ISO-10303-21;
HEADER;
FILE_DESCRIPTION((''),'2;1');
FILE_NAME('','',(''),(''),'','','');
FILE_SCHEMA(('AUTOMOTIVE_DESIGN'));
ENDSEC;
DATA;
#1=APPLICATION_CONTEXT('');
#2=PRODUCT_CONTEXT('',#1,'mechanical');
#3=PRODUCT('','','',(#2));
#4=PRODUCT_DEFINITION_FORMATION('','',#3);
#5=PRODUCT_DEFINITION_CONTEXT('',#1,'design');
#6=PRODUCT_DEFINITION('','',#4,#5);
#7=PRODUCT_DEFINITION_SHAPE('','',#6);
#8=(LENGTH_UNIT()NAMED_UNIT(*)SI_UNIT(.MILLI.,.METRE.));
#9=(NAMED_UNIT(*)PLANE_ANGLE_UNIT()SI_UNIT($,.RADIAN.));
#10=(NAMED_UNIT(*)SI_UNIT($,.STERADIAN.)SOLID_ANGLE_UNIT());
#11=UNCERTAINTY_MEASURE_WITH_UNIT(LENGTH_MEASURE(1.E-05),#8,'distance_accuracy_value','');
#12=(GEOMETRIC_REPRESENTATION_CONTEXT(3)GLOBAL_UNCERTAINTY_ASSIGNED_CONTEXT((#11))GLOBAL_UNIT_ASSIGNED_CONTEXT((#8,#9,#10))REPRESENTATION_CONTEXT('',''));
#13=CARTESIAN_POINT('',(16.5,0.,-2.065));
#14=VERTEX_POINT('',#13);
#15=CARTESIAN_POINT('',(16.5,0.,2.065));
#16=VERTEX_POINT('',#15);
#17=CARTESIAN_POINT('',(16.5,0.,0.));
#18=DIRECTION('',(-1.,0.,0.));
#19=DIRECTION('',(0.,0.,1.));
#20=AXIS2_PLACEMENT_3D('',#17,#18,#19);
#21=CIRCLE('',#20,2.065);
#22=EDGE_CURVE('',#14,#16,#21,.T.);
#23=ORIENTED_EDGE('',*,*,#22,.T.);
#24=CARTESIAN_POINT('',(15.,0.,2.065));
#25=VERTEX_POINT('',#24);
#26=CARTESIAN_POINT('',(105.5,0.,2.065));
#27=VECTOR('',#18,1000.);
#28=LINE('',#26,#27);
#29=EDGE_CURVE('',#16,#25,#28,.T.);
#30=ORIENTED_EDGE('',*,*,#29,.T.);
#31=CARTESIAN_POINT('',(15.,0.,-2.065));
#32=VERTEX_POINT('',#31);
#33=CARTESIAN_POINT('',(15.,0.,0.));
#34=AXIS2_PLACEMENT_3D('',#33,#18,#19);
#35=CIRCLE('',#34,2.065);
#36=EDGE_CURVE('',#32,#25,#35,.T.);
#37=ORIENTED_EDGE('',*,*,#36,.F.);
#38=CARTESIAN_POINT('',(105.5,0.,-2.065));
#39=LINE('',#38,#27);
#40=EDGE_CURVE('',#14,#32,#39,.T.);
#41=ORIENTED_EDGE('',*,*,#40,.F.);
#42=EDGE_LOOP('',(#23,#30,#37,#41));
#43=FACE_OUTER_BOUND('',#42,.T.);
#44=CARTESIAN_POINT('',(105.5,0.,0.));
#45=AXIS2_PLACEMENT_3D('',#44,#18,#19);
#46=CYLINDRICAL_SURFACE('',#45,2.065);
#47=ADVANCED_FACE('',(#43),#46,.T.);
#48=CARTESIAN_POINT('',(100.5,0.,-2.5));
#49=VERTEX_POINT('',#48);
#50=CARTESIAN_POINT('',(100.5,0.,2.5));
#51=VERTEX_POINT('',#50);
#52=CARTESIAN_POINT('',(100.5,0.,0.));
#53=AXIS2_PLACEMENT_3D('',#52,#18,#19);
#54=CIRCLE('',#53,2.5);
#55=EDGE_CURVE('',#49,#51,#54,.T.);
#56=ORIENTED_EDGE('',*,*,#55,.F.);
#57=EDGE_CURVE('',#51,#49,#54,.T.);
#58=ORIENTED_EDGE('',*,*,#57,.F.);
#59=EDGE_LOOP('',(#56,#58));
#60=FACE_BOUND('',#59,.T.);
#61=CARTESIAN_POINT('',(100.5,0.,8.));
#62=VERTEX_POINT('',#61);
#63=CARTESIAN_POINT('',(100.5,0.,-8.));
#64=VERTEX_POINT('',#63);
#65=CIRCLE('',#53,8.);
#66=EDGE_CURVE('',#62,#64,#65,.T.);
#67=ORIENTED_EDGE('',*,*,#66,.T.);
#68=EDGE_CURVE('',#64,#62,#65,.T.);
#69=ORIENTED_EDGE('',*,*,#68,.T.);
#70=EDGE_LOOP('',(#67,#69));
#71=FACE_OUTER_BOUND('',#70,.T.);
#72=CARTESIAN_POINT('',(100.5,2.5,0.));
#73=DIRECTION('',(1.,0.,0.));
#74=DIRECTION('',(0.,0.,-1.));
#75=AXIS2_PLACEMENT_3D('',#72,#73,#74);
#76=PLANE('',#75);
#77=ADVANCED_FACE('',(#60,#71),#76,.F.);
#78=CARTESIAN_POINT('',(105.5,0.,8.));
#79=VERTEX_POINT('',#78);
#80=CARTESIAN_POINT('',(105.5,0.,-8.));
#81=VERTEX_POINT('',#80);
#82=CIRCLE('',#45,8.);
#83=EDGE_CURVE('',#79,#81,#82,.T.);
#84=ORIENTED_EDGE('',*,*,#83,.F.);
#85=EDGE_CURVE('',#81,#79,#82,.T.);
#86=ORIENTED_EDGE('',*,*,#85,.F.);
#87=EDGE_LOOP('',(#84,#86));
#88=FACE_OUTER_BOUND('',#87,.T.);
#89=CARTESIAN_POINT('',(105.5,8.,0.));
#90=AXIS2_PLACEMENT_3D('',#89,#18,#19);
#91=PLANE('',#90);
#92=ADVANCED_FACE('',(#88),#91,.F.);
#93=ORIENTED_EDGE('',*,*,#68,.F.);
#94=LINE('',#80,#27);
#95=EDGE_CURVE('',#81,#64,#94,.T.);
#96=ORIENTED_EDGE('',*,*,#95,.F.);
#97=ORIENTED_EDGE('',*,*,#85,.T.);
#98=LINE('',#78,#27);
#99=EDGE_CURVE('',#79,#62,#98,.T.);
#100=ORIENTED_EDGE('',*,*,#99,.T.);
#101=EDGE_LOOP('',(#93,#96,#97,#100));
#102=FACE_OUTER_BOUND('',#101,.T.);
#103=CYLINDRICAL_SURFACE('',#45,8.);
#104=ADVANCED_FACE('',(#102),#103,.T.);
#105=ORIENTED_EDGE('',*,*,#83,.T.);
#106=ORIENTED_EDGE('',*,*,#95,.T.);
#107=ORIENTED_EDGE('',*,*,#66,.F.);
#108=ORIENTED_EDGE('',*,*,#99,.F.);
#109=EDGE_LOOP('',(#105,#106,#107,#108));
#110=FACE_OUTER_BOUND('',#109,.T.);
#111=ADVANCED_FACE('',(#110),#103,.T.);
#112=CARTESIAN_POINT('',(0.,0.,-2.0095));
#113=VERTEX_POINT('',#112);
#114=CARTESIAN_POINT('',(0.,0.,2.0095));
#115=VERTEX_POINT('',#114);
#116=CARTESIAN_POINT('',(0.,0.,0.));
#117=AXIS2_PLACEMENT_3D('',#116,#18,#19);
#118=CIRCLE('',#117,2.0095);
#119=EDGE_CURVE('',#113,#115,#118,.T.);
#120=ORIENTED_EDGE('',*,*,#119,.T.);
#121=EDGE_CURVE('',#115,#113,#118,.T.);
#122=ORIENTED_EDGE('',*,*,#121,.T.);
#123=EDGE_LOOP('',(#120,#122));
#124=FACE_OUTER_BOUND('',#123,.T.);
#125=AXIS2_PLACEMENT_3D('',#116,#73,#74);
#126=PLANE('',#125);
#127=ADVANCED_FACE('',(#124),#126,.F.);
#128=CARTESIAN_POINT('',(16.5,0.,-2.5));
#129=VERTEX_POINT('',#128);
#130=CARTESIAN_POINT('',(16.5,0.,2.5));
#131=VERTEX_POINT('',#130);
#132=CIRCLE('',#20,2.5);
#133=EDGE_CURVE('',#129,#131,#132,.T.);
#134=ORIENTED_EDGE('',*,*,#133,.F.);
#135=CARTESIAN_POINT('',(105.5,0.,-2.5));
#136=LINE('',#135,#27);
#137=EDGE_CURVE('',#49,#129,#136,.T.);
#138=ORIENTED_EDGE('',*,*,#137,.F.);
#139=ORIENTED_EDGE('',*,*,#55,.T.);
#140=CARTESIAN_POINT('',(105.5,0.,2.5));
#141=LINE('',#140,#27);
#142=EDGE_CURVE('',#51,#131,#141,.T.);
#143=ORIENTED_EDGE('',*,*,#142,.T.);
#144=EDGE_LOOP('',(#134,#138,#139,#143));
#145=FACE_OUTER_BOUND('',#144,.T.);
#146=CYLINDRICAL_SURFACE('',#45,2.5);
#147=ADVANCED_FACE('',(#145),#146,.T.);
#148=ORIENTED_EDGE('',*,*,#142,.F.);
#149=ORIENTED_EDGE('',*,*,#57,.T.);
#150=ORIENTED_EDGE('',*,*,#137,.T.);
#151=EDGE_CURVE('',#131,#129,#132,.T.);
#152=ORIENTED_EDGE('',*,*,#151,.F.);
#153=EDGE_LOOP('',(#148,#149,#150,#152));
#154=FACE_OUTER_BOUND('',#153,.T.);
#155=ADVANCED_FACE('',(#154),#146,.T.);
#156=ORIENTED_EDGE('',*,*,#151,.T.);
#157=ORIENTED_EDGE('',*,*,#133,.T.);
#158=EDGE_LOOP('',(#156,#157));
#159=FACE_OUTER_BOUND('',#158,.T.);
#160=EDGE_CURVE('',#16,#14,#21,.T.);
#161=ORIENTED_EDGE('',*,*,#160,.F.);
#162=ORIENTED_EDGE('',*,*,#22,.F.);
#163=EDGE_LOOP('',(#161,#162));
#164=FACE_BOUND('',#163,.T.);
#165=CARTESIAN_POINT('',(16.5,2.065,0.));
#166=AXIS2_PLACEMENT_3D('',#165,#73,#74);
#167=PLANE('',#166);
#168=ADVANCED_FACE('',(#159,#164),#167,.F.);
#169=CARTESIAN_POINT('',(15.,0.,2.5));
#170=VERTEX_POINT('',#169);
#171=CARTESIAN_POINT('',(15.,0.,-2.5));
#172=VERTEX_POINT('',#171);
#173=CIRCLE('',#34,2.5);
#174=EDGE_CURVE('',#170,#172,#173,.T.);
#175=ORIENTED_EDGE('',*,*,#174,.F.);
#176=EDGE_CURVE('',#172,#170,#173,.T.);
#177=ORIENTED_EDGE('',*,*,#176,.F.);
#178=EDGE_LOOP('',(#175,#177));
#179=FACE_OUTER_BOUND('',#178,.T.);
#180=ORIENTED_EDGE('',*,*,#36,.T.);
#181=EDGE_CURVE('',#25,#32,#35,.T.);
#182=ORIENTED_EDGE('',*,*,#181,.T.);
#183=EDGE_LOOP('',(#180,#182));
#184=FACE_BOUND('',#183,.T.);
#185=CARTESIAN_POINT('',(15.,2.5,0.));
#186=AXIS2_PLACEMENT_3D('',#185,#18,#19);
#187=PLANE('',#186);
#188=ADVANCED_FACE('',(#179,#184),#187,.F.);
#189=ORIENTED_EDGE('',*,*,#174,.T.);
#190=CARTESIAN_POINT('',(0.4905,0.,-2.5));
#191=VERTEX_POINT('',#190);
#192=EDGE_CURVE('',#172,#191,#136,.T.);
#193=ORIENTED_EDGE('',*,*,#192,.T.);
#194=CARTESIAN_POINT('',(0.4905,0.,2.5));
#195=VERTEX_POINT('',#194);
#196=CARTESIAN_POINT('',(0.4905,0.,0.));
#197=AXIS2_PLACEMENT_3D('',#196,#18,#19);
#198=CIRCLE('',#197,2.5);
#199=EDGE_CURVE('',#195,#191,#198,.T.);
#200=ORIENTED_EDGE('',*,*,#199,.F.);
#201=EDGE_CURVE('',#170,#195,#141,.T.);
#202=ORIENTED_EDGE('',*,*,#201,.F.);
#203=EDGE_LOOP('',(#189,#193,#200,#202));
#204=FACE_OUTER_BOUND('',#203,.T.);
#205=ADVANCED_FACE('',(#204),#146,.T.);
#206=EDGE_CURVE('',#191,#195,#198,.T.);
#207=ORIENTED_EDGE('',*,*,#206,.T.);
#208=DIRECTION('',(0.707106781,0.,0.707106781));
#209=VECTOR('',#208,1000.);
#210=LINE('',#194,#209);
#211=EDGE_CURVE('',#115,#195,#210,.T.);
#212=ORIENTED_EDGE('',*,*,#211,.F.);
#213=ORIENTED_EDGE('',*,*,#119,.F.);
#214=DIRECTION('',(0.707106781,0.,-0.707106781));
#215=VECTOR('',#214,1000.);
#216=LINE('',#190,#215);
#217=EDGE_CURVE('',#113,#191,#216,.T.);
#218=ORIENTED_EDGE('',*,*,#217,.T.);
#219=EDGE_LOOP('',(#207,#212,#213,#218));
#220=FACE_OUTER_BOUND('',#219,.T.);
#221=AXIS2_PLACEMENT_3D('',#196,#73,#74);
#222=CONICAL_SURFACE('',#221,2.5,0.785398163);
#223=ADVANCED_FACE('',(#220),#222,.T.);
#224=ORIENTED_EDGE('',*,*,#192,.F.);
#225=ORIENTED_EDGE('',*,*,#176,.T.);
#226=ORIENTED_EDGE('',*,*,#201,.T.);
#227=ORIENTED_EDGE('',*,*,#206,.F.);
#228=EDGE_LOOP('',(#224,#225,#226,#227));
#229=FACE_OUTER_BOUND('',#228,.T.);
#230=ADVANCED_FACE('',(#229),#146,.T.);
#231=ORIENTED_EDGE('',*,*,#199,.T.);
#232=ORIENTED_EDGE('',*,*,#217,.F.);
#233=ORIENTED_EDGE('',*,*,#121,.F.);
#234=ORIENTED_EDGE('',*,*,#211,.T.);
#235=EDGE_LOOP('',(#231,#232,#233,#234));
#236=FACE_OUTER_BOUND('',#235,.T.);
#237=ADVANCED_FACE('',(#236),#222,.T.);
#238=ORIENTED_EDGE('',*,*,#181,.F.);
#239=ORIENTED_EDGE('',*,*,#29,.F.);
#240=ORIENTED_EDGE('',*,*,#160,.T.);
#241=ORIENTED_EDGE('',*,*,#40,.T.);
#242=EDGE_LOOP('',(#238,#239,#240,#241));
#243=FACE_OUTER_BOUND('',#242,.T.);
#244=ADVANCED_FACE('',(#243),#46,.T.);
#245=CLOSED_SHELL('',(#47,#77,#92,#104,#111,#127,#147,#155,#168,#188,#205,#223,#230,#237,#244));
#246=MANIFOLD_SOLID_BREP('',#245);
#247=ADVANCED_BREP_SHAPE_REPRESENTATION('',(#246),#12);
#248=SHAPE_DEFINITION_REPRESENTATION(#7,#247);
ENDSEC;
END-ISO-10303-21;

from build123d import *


with BuildPart() as part:
    # 草图1 → 旋转1 (revolve)
    with BuildSketch(Plane.XY, mode=Mode.PRIVATE) as revolve_1_sk:
        Polygon((0, 0), (0, 2.0095), (0.4905, 2.5), (15, 2.5), (15, 2.065), (16.5, 2.065), (16.5, 2.5), (100.5, 2.5), (100.5, 8), (105.5, 8), (105.5, 0), align=None)
    revolve(revolve_1_sk.sketch.rotate(Axis((105.5, 0, 0), (-1, 0, 0)), 270), axis=Axis((105.5, 0, 0), (-1, 0, 0)))


solid = part.part
